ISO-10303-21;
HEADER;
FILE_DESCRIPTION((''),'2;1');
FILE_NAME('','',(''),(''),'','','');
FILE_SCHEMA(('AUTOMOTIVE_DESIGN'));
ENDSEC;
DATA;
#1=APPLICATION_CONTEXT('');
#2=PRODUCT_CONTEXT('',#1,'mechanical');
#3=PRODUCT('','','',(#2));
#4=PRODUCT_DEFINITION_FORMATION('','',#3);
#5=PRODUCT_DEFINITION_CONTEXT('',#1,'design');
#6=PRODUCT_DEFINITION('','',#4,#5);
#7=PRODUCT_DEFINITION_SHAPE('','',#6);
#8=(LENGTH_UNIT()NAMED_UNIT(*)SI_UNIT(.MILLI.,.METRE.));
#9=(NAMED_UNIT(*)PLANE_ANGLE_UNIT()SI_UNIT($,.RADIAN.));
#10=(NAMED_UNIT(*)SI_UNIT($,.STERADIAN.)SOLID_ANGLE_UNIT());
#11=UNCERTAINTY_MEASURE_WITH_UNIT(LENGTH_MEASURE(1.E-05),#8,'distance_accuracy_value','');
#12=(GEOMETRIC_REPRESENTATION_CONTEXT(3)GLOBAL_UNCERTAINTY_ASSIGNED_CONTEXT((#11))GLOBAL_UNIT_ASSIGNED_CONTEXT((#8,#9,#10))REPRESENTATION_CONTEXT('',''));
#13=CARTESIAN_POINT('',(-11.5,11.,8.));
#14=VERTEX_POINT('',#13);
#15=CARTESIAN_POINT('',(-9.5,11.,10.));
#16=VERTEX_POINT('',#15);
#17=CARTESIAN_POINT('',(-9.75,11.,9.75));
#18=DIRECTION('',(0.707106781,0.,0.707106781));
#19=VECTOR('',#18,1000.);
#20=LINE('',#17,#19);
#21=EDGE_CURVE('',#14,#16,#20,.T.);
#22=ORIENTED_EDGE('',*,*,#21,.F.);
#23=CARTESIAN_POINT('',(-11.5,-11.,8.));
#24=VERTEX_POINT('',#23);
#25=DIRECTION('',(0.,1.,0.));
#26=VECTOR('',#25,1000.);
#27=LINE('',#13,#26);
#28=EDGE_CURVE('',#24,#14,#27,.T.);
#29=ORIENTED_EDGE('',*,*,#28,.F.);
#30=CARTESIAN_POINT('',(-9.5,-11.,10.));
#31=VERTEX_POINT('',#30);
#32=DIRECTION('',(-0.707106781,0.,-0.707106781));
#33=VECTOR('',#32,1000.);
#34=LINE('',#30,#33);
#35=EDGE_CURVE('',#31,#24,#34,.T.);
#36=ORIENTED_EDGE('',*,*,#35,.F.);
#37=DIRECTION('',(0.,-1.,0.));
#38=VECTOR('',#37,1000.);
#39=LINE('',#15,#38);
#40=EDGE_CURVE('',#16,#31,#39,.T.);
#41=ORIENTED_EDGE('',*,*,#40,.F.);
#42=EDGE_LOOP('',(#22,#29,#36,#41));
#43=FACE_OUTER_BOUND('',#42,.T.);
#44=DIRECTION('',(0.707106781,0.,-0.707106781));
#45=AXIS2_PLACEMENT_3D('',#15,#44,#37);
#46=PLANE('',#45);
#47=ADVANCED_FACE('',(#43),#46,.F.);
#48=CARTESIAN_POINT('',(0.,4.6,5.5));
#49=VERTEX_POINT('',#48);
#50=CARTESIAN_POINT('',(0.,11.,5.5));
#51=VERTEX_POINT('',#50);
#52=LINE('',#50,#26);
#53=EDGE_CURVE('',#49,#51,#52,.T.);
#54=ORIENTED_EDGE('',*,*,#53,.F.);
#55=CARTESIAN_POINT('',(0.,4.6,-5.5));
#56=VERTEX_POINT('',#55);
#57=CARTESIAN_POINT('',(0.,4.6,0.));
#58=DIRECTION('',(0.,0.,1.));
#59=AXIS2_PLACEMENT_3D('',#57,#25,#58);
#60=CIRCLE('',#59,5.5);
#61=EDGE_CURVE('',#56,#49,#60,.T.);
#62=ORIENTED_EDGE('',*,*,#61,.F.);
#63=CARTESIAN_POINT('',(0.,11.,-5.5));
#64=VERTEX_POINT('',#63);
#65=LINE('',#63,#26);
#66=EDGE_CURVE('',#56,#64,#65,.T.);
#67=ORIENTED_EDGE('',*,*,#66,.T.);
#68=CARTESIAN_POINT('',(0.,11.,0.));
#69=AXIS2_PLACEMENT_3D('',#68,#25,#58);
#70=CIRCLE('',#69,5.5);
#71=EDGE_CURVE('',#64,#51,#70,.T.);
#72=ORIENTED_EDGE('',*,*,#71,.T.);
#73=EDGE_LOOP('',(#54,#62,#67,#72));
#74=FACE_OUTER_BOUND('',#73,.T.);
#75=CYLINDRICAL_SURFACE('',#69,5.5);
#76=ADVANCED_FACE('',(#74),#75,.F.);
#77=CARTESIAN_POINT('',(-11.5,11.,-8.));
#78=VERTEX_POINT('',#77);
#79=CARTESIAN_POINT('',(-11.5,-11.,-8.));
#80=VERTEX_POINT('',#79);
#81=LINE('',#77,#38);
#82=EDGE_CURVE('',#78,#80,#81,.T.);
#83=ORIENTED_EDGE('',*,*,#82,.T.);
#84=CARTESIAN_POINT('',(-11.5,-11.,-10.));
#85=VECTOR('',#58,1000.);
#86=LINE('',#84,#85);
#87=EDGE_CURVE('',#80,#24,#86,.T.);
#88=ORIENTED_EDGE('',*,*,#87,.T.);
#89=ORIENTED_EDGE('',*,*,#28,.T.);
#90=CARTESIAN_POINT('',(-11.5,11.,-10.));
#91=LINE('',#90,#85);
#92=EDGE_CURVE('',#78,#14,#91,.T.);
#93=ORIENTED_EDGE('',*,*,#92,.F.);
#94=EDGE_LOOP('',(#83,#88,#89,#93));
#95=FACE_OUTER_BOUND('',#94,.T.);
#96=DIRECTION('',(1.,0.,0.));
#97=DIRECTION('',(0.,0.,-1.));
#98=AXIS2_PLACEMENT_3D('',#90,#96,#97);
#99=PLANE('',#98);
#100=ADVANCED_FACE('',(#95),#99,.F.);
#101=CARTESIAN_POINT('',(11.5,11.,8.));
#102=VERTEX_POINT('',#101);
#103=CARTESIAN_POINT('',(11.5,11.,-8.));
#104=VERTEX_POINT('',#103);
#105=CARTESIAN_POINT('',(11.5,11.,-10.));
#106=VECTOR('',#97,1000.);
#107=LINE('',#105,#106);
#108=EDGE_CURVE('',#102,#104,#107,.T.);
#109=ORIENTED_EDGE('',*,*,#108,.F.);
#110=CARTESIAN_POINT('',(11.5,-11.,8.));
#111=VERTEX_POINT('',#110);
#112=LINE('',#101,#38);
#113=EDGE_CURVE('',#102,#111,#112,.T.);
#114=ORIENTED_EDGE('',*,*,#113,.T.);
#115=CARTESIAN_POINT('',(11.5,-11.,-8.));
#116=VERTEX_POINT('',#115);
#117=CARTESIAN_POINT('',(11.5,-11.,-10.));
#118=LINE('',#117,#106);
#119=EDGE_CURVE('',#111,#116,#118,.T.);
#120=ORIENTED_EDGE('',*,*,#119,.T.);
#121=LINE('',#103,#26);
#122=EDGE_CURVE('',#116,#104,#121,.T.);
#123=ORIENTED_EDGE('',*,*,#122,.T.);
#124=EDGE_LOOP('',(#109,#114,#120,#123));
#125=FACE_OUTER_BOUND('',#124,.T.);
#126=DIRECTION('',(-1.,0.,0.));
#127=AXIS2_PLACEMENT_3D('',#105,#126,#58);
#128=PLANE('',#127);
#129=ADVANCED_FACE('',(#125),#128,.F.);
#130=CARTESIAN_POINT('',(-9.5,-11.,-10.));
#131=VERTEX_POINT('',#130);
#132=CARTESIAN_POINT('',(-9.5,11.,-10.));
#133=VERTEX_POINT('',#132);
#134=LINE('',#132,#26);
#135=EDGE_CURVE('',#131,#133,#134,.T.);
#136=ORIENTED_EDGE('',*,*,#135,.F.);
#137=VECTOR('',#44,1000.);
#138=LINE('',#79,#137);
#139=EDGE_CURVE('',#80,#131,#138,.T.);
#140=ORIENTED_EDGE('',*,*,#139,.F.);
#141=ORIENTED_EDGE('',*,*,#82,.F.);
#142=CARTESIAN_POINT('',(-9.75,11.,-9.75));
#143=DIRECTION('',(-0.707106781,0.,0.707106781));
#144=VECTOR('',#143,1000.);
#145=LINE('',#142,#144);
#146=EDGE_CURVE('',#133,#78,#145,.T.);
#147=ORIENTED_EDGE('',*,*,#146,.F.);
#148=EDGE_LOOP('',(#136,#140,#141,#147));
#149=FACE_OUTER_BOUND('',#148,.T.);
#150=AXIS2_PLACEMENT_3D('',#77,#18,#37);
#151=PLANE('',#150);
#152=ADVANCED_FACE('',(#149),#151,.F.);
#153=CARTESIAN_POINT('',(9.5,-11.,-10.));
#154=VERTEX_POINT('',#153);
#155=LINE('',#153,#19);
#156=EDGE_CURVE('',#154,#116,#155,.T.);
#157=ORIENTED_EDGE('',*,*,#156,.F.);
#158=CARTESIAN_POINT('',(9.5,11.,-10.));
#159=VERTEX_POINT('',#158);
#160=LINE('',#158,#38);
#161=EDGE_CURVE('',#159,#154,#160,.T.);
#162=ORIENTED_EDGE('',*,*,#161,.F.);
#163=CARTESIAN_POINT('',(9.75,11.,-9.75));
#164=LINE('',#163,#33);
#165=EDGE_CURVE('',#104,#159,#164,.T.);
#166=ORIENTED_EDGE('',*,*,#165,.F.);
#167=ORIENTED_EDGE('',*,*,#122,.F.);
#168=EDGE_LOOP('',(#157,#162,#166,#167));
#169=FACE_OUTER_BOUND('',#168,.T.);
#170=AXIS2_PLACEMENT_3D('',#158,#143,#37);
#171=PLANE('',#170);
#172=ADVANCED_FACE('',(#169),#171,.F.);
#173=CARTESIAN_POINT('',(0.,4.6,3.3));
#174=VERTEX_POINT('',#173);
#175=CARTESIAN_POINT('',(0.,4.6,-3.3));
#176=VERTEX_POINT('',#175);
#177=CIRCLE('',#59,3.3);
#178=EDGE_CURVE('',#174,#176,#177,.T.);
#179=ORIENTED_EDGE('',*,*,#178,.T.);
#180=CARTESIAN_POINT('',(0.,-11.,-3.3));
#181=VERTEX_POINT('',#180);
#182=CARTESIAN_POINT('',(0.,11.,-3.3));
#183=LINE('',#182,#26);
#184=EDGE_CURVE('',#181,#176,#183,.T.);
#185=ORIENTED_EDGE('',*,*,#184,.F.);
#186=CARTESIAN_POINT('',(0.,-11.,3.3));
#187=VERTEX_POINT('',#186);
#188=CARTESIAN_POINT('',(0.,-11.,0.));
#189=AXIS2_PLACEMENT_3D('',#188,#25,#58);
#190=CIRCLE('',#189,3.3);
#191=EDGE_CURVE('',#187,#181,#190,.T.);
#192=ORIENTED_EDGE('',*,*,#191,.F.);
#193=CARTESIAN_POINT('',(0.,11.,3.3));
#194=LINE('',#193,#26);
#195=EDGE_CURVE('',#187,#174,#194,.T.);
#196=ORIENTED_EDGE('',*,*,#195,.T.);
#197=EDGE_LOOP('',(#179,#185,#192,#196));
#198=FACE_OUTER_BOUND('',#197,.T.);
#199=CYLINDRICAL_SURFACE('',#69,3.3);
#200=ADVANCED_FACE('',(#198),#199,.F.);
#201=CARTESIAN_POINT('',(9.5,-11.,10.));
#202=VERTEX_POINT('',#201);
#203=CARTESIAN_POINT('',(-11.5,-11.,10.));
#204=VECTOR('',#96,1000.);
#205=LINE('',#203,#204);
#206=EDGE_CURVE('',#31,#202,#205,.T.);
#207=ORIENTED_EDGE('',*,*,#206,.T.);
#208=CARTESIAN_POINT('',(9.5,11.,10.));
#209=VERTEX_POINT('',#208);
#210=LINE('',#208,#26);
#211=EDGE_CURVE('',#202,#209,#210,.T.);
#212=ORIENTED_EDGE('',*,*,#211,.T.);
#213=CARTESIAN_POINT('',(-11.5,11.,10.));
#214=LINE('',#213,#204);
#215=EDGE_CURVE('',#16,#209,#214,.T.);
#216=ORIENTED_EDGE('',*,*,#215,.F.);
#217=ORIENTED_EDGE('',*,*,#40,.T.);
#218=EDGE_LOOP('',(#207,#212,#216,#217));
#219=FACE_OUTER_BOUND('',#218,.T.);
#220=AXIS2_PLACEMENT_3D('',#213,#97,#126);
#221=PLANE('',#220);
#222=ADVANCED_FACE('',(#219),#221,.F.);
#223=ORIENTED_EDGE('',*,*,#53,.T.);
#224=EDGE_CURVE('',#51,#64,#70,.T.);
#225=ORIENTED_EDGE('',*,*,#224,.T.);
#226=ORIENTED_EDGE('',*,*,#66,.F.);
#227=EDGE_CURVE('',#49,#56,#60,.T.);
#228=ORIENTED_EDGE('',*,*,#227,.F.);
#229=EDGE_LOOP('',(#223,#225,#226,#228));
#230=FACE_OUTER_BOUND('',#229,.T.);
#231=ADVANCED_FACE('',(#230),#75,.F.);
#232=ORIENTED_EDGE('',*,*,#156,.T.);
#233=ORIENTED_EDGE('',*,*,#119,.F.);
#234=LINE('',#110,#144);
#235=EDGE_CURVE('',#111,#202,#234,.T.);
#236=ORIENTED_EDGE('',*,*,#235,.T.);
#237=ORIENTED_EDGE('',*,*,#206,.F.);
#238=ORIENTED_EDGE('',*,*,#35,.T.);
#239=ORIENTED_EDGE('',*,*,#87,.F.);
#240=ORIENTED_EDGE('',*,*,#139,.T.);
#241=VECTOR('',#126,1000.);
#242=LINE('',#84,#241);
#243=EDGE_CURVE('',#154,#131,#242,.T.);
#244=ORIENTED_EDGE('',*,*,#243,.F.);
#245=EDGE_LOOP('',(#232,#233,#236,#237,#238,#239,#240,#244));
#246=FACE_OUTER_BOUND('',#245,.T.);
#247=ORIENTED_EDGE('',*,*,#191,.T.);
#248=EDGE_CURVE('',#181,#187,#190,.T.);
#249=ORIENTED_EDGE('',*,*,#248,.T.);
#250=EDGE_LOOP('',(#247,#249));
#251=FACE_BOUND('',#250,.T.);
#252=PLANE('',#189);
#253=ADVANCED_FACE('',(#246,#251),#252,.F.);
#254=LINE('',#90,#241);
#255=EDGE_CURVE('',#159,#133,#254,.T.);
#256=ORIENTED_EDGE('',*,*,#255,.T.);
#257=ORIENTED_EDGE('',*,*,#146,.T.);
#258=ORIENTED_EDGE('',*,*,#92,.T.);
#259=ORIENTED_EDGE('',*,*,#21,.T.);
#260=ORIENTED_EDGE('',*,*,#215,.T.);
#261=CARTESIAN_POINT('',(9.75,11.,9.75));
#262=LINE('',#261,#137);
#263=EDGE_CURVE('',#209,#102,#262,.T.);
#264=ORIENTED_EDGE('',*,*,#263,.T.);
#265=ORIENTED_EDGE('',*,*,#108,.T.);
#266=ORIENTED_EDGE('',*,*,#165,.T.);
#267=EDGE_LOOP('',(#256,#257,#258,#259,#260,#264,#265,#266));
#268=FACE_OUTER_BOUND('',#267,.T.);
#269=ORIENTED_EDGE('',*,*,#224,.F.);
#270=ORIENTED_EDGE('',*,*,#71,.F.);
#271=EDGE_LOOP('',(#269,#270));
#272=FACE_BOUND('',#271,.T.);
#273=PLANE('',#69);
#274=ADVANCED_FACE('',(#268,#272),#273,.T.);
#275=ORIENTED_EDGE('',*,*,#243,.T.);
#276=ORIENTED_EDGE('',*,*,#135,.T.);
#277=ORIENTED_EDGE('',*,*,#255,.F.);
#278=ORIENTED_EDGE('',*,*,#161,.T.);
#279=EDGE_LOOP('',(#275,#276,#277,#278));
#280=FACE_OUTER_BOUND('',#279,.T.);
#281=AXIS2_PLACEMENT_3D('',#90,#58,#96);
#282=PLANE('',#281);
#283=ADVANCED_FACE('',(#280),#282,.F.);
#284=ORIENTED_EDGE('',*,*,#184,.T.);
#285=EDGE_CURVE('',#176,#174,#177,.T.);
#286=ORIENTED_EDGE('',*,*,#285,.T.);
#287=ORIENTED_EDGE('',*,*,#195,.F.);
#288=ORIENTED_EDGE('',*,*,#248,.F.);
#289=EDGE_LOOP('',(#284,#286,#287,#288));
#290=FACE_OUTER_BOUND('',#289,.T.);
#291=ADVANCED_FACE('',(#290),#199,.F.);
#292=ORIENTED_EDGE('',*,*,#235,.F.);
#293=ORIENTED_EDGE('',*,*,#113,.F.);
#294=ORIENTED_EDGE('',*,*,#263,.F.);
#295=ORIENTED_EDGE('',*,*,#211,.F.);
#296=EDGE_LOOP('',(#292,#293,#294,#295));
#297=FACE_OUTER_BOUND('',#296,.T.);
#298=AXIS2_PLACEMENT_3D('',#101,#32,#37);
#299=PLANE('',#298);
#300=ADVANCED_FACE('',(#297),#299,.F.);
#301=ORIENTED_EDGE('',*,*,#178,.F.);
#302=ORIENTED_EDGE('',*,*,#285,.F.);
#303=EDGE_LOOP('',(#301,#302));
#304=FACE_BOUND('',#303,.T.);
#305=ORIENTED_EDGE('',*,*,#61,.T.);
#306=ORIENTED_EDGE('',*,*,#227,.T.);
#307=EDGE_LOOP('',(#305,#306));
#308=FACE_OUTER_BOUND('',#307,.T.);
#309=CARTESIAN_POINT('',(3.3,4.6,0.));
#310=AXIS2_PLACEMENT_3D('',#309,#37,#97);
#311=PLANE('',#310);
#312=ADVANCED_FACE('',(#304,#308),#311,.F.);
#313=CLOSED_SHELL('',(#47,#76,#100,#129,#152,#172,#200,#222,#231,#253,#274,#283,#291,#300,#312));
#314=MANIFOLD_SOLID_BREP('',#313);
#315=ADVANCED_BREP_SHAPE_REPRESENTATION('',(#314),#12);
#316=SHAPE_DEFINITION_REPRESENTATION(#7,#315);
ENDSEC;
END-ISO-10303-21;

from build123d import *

# Parameters (mm, degrees)
SKETCH_1_W                   = 23
SKETCH_1_H                   = 20
EXTRUDE_1_DEPTH              = 11
HOLE_WIZARD_M6_1_D           = 6.6
HOLE_WIZARD_M6_1_CBORE_D     = 11
HOLE_WIZARD_M6_1_CBORE_DEPTH = 6.4
CHAMFER_1_SIZE               = 2


with BuildPart() as part:
    # 草图1 → 凸台-拉伸1 (new, symmetric)
    with BuildSketch(Plane(origin=(0, 0, 0), x_dir=(1, 0, 0), z_dir=(0, 1, 0))):
        Rectangle(SKETCH_1_W, SKETCH_1_H)
    extrude(amount=EXTRUDE_1_DEPTH, both=True)

    # M6 六角凹头螺钉的柱形沉头孔1 (through all)
    with Locations(Plane(origin=(0, 11, 0), x_dir=(1, 0, 0), z_dir=(0, 1, 0))):
        with Locations((0, 0)):
            CounterBoreHole(HOLE_WIZARD_M6_1_D / 2, HOLE_WIZARD_M6_1_CBORE_D / 2, HOLE_WIZARD_M6_1_CBORE_DEPTH)

    # 倒角1
    chamfer_1_edges = [part.edges().sort_by_distance(p)[0] for p in [
        (-11.5, 0, -10),
        (11.5, 0, -10),
        (11.5, 0, 10),
        (-11.5, 0, 10),
    ]]
    chamfer(chamfer_1_edges, length=CHAMFER_1_SIZE)


solid = part.part
